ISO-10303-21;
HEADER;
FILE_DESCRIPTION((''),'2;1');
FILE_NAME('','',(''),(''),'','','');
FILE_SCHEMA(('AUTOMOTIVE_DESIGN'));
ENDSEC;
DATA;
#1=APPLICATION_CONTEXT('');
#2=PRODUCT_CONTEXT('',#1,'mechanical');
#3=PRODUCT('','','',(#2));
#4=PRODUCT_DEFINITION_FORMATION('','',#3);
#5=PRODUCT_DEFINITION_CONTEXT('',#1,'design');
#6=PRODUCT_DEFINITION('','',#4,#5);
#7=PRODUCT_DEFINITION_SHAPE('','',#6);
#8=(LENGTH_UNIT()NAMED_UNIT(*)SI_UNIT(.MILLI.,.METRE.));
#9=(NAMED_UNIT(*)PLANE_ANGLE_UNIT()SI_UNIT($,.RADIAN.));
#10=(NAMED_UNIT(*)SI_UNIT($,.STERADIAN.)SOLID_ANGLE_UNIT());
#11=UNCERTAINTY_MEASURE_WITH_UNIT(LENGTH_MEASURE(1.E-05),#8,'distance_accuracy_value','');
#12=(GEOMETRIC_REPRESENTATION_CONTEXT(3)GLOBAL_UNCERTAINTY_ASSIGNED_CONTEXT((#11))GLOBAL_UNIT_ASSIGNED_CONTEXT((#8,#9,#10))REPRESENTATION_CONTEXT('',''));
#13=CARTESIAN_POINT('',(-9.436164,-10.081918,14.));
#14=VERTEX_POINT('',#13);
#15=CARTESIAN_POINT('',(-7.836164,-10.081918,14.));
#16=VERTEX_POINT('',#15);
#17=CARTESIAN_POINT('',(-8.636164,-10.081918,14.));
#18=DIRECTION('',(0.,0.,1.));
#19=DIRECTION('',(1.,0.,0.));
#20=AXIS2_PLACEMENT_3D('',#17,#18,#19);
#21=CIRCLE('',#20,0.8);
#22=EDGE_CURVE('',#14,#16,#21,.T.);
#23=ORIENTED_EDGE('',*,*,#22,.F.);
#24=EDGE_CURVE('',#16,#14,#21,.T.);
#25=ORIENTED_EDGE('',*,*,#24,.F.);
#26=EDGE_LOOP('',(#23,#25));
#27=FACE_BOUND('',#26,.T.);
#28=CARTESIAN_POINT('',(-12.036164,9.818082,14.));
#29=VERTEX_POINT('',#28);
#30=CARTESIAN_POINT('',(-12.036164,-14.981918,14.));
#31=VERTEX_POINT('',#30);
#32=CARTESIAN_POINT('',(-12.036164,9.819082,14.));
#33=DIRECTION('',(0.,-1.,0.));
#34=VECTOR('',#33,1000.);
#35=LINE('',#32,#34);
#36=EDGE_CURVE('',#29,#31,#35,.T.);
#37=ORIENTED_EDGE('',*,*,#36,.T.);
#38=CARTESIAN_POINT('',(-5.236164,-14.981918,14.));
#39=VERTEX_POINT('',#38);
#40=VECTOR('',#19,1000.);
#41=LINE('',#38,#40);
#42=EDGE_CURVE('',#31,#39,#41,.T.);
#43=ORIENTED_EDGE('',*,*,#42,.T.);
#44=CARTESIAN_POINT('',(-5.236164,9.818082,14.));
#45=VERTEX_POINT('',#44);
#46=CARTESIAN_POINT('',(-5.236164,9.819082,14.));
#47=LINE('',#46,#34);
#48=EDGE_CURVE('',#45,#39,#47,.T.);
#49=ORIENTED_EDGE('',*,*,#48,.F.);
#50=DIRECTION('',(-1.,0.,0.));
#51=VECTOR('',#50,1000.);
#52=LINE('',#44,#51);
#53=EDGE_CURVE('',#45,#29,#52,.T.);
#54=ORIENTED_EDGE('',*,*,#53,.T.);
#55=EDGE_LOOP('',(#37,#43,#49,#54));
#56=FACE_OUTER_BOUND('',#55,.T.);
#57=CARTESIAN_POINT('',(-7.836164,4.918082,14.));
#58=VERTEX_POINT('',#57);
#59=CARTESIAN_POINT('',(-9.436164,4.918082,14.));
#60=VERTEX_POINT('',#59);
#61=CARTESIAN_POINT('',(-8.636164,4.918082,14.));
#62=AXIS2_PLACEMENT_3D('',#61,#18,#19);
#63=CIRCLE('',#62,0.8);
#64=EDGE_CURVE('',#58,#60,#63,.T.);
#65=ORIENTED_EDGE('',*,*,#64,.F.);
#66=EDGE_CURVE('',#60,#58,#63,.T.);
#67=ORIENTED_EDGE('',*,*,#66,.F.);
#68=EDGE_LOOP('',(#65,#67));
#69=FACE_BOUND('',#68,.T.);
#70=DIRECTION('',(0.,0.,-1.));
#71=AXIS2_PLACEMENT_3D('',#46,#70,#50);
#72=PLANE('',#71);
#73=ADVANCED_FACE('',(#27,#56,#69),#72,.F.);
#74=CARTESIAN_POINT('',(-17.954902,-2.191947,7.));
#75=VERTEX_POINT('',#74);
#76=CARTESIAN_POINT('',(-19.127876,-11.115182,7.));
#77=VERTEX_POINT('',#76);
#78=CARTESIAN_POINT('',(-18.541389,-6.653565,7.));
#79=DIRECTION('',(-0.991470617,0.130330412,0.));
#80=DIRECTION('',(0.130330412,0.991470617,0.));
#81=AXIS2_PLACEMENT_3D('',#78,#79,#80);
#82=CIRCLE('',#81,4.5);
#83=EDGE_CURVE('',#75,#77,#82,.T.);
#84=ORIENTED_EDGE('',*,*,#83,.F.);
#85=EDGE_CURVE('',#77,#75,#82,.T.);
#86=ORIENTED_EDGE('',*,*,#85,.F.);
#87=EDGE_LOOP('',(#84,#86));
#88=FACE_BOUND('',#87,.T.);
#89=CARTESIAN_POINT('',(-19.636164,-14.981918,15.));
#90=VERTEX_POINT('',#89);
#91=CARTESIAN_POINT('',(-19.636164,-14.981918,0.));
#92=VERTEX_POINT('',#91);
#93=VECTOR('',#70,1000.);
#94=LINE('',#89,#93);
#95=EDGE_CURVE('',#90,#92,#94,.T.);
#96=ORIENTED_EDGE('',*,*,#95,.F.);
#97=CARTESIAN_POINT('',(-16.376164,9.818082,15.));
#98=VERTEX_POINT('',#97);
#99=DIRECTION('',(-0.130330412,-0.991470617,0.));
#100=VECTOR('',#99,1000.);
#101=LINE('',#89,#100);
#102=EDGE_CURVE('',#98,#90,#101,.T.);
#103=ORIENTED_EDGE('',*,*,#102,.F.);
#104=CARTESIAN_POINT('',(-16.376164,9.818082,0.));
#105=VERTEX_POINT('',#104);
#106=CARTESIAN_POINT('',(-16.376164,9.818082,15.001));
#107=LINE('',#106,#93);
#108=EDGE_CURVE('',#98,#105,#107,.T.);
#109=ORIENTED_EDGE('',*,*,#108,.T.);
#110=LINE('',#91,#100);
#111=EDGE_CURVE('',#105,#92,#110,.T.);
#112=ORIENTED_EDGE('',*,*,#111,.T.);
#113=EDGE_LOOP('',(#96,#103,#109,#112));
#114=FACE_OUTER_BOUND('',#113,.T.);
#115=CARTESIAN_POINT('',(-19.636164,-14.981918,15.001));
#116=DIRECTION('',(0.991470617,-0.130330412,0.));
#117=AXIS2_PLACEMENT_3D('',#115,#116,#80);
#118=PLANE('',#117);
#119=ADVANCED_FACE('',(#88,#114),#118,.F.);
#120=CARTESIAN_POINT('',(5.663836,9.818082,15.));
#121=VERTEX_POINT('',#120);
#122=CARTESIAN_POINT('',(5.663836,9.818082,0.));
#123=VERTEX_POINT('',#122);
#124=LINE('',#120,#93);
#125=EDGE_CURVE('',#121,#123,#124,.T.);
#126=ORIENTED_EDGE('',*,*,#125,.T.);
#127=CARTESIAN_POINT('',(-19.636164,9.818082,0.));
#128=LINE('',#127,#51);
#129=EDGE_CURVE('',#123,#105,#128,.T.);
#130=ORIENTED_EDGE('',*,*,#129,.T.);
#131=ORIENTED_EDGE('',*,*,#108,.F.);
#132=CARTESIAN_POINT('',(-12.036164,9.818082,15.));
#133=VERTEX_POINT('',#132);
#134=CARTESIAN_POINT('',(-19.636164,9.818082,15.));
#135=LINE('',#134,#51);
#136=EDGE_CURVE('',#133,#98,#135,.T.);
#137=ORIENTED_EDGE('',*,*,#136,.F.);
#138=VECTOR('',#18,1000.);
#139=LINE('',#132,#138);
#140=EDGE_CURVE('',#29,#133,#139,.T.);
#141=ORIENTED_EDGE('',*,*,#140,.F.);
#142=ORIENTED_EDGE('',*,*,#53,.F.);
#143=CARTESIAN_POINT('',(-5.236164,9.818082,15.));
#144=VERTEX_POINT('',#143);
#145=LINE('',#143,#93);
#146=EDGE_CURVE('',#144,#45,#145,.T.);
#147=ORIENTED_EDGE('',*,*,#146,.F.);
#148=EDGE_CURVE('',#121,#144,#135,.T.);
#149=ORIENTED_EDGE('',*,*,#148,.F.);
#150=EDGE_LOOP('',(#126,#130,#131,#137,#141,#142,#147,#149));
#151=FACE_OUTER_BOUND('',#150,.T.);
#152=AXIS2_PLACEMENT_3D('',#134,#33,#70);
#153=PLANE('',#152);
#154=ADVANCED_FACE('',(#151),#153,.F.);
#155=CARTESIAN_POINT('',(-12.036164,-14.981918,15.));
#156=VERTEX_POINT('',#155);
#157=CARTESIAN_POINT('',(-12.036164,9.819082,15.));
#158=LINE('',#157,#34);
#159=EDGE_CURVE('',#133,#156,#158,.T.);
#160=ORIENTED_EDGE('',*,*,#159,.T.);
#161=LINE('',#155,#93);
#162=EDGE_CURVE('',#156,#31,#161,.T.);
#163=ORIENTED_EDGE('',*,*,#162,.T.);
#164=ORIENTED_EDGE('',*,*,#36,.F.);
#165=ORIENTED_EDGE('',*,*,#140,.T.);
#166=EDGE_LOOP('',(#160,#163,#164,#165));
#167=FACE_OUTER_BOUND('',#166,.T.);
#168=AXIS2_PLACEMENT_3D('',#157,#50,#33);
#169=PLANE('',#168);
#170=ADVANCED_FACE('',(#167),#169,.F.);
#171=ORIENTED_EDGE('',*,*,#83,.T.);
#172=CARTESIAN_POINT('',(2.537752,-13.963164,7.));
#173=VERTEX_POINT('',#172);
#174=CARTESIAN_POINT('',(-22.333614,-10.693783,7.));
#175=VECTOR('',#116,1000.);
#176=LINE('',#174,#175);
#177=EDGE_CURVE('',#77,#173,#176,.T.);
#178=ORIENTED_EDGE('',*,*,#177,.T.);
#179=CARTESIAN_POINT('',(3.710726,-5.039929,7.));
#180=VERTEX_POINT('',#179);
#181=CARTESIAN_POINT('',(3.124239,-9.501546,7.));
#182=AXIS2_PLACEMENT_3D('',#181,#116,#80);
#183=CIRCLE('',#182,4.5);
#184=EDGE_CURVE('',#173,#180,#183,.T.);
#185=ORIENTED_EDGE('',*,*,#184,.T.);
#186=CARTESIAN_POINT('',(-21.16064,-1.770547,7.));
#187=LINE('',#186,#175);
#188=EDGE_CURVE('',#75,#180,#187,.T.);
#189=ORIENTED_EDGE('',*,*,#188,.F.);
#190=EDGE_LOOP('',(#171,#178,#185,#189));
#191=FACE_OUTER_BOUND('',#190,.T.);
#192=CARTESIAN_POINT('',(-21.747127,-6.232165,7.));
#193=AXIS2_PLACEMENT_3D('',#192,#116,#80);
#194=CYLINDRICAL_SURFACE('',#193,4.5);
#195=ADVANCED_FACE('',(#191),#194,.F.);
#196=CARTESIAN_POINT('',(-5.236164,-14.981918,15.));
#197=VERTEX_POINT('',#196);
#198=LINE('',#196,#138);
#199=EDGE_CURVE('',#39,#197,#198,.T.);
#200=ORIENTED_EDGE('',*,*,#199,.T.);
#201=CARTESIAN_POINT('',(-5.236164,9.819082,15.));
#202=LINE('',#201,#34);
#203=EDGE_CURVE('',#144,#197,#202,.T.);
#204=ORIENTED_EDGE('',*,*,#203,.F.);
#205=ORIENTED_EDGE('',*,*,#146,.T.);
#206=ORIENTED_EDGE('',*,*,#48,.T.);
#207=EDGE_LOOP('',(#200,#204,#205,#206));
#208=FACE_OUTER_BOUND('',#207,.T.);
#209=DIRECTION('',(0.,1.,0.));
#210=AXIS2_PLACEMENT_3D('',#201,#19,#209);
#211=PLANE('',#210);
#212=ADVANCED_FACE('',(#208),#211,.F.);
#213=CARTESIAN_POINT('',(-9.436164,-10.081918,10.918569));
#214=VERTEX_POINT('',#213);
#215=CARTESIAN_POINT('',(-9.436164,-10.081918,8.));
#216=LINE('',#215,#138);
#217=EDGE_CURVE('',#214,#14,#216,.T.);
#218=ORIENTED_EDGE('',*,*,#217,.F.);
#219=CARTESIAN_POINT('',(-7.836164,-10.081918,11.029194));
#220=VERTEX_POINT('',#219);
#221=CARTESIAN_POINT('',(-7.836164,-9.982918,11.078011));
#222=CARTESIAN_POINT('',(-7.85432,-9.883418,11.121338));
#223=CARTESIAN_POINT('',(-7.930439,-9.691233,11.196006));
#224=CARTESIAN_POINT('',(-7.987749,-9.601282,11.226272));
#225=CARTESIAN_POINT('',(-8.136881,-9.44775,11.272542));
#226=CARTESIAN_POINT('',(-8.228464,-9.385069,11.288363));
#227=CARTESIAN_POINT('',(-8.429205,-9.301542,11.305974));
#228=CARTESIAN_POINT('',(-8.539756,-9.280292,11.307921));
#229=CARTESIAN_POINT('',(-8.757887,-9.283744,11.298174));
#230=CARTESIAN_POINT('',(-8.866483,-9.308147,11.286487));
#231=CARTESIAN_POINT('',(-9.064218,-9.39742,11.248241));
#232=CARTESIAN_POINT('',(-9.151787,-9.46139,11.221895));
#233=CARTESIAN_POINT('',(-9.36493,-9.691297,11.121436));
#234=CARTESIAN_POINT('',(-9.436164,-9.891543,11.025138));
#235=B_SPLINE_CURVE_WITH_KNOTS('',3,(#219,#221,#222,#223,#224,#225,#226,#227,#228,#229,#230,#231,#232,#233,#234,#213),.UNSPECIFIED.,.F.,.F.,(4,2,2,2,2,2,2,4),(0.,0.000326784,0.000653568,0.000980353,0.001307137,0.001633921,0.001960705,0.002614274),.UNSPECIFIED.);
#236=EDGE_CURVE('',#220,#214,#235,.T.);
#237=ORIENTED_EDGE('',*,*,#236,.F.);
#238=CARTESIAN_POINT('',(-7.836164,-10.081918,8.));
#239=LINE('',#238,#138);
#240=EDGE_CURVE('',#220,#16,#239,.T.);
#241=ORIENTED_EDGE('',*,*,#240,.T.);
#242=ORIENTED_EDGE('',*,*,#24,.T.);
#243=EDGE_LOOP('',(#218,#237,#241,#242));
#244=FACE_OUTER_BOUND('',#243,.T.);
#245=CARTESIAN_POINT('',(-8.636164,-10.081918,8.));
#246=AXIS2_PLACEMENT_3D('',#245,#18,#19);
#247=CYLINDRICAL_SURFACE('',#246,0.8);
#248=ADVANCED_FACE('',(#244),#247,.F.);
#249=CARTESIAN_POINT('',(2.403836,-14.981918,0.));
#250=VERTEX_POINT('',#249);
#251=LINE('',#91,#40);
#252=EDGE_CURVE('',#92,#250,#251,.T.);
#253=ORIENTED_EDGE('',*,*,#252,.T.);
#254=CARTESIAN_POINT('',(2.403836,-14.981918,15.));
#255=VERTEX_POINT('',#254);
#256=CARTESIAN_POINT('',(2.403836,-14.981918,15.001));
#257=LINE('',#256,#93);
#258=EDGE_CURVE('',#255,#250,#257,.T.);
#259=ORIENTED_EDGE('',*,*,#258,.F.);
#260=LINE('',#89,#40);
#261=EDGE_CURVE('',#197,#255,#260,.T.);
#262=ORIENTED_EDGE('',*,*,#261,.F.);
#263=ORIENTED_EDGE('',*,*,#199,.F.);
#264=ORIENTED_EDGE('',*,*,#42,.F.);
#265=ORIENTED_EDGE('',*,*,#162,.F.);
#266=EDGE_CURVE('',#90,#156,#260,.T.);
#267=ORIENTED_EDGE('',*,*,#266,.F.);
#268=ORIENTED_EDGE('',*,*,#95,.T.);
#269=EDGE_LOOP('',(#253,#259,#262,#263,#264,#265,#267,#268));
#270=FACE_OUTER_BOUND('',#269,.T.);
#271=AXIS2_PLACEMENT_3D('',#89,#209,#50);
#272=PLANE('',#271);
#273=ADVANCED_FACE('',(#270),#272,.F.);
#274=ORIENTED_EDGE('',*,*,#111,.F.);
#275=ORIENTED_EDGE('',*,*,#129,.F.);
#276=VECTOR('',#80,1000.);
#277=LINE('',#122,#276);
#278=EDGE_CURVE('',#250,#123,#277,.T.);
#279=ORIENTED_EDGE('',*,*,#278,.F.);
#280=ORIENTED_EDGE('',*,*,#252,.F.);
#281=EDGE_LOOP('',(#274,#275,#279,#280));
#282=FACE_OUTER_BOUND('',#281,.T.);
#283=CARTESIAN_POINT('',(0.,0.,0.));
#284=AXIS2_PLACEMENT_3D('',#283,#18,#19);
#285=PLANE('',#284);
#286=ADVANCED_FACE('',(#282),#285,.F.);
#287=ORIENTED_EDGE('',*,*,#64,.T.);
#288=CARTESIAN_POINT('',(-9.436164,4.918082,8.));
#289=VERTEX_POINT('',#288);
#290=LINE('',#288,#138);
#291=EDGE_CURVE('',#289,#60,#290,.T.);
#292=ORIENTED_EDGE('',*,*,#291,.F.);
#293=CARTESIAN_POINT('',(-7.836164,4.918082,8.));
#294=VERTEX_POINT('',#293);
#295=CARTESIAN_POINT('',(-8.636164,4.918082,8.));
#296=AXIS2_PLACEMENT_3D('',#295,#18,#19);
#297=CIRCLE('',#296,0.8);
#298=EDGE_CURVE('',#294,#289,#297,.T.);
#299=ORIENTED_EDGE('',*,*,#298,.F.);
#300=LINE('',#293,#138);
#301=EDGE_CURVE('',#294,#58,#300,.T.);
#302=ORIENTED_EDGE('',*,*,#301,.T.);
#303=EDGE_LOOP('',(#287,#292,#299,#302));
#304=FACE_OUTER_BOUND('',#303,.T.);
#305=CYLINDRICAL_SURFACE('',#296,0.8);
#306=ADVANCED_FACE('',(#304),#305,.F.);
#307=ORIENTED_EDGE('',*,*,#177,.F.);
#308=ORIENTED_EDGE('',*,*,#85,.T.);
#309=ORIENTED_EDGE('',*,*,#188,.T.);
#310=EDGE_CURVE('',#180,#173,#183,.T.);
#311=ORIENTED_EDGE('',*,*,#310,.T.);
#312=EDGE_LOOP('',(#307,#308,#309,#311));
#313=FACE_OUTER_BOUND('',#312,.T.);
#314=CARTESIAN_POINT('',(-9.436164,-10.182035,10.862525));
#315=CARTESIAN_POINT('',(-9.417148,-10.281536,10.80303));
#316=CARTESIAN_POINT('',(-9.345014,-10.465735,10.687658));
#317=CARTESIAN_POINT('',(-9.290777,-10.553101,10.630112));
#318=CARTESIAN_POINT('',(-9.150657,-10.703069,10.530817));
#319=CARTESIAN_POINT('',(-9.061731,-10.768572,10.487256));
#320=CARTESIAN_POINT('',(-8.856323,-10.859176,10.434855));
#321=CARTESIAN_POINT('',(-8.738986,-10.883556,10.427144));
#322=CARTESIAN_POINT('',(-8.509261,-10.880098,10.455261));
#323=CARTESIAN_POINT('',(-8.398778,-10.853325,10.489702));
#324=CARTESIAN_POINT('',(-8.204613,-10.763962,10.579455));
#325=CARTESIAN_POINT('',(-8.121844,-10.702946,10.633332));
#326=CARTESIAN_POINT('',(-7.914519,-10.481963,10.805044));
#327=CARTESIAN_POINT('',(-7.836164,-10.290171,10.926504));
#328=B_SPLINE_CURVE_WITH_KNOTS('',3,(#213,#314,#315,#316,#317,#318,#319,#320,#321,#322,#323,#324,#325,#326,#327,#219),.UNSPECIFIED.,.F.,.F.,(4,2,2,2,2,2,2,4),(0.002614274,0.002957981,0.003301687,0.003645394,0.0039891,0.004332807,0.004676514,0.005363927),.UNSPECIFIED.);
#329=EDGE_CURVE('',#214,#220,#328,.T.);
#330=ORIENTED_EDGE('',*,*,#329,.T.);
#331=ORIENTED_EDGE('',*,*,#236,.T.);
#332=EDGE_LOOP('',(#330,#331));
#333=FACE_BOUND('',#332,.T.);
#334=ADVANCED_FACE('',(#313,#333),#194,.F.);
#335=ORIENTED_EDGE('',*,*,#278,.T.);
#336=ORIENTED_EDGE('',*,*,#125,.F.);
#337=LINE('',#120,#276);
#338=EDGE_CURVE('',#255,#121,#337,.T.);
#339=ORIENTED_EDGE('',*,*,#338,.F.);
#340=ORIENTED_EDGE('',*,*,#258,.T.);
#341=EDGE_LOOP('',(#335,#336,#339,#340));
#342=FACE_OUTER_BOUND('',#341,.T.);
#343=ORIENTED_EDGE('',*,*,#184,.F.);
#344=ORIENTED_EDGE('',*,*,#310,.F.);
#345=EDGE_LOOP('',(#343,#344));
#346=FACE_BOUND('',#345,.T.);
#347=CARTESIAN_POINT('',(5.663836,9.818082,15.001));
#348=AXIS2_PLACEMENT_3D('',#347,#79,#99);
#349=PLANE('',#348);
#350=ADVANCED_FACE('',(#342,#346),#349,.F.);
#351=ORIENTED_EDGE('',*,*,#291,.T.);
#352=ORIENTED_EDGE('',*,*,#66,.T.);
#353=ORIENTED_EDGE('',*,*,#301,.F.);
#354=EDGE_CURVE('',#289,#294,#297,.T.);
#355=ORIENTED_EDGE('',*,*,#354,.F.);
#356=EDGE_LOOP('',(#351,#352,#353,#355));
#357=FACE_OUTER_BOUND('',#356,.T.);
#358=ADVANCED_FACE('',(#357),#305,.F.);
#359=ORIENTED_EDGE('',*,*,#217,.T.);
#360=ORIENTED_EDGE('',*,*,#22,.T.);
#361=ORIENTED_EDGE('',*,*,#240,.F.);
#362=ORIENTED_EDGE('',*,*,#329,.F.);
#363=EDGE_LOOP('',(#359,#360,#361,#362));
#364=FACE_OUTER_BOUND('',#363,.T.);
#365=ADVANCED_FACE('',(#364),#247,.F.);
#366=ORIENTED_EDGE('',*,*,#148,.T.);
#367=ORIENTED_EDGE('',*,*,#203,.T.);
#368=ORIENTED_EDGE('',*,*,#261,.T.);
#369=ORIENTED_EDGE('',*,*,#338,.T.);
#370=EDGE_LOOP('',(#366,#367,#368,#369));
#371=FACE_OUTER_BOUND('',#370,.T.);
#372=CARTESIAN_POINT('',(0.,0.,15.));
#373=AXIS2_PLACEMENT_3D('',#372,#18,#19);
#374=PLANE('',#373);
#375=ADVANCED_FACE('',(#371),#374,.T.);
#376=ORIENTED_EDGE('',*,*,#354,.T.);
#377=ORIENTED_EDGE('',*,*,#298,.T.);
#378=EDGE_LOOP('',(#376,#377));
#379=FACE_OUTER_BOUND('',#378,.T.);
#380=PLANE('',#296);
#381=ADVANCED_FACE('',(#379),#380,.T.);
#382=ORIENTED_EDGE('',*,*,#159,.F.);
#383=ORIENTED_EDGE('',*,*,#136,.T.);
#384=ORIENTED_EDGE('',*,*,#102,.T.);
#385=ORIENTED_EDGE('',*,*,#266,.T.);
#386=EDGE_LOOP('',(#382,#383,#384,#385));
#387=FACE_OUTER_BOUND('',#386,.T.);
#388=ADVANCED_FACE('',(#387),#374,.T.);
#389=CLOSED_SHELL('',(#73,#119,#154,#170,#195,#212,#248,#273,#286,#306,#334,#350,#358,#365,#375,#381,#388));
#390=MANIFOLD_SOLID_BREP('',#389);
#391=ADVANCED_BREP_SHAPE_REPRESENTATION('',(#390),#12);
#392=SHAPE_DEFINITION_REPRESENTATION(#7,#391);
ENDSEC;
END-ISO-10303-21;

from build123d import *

# Parameters (mm, degrees)
SKETCH_1_W          = 25.3
SKETCH_1_H          = 24.8
EXTRUDE_1_DEPTH     = 15
CUT_EXTRUDE_1_REACH = 30.897
CUT_EXTRUDE_2_REACH = 37.009
SKETCH_3_W          = 6.8
SKETCH_3_H          = 1
CUT_EXTRUDE_3_REACH = 33.713
SKETCH_5_R          = 4.5
SKETCH_7_R          = 0.8
CUT_EXTRUDE_4_DEPTH = 6


with BuildPart() as part:
    # 草图1 → 凸台-拉伸1 (new body)
    with BuildSketch(Plane.XY):
        with Locations((-6.986164384, -2.581917808)):
            Rectangle(SKETCH_1_W, SKETCH_1_H)
    extrude(amount=EXTRUDE_1_DEPTH)

    # 草图2 → 切除-拉伸1 (cut, up to next)
    with BuildSketch(Plane(origin=(0, 0, 0), x_dir=(-1, 0, 0), z_dir=(0, 0, -1)), mode=Mode.PRIVATE) as cut_extrude_1_sk1:
        Polygon((-5.663835616, 9.818082192), (-2.403835616, -14.981917808), (-5.663835616, -14.981917808), align=None)
    cut_extrude_1_tool1 = extrude(cut_extrude_1_sk1.sketch, amount=-CUT_EXTRUDE_1_REACH, mode=Mode.PRIVATE) & part.part
    # 草图2 → 切除-拉伸1 (cut, up to next)
    with BuildSketch(Plane(origin=(0, 0, 0), x_dir=(-1, 0, 0), z_dir=(0, 0, -1)), mode=Mode.PRIVATE) as cut_extrude_1_sk2:
        Polygon((16.376164384, 9.818082192), (19.636164384, 9.818082192), (19.636164384, -14.981917808), align=None)
    cut_extrude_1_tool2 = extrude(cut_extrude_1_sk2.sketch, amount=-CUT_EXTRUDE_1_REACH, mode=Mode.PRIVATE) & part.part
    add(cut_extrude_1_tool1.solids().sort_by_distance((4.577169, -6.715251, 0))[0], mode=Mode.SUBTRACT)
    add(cut_extrude_1_tool2.solids().sort_by_distance((-18.549498, 1.551416, 0))[0], mode=Mode.SUBTRACT)

    # 草图3 → 切除-拉伸2 (cut, up to next)
    with BuildSketch(Plane.XZ.offset(14.981917808), mode=Mode.PRIVATE) as cut_extrude_2_sk1:
        with Locations((-8.636164384, 14.5)):
            Rectangle(SKETCH_3_W, SKETCH_3_H)
    cut_extrude_2_tool1 = extrude(cut_extrude_2_sk1.sketch, amount=-CUT_EXTRUDE_2_REACH, mode=Mode.PRIVATE) & part.part
    add(cut_extrude_2_tool1.solids().sort_by_distance((-8.636164, -14.981918, 14.5))[0], mode=Mode.SUBTRACT)

    # 草图5 → 切除-拉伸3 (cut, up to next)
    with BuildSketch(Plane(origin=(4.298949072, -0.565103789, 0), x_dir=(0, 0, -1), z_dir=(0.9914706167018176, -0.13033041171160964, 0)), mode=Mode.PRIVATE) as cut_extrude_3_sk1:
        with Locations(Location((-7, -9.013320677, 0), (0, 0, 90))):
            Circle(SKETCH_5_R)
    cut_extrude_3_tool1 = extrude(cut_extrude_3_sk1.sketch, amount=-CUT_EXTRUDE_3_REACH, mode=Mode.PRIVATE) & part.part
    add(cut_extrude_3_tool1.solids().sort_by_distance((3.124239, -9.501546, 7))[0], mode=Mode.SUBTRACT)

    # 草图7 → 切除-拉伸4 (cut)
    with BuildSketch(Plane.XY.offset(14)):
        with Locations((-8.636164384, 4.918082192)):
            Circle(SKETCH_7_R)
        with Locations((-8.636164384, -10.081917808)):
            Circle(SKETCH_7_R)
    extrude(amount=-CUT_EXTRUDE_4_DEPTH, mode=Mode.SUBTRACT)


solid = part.part
